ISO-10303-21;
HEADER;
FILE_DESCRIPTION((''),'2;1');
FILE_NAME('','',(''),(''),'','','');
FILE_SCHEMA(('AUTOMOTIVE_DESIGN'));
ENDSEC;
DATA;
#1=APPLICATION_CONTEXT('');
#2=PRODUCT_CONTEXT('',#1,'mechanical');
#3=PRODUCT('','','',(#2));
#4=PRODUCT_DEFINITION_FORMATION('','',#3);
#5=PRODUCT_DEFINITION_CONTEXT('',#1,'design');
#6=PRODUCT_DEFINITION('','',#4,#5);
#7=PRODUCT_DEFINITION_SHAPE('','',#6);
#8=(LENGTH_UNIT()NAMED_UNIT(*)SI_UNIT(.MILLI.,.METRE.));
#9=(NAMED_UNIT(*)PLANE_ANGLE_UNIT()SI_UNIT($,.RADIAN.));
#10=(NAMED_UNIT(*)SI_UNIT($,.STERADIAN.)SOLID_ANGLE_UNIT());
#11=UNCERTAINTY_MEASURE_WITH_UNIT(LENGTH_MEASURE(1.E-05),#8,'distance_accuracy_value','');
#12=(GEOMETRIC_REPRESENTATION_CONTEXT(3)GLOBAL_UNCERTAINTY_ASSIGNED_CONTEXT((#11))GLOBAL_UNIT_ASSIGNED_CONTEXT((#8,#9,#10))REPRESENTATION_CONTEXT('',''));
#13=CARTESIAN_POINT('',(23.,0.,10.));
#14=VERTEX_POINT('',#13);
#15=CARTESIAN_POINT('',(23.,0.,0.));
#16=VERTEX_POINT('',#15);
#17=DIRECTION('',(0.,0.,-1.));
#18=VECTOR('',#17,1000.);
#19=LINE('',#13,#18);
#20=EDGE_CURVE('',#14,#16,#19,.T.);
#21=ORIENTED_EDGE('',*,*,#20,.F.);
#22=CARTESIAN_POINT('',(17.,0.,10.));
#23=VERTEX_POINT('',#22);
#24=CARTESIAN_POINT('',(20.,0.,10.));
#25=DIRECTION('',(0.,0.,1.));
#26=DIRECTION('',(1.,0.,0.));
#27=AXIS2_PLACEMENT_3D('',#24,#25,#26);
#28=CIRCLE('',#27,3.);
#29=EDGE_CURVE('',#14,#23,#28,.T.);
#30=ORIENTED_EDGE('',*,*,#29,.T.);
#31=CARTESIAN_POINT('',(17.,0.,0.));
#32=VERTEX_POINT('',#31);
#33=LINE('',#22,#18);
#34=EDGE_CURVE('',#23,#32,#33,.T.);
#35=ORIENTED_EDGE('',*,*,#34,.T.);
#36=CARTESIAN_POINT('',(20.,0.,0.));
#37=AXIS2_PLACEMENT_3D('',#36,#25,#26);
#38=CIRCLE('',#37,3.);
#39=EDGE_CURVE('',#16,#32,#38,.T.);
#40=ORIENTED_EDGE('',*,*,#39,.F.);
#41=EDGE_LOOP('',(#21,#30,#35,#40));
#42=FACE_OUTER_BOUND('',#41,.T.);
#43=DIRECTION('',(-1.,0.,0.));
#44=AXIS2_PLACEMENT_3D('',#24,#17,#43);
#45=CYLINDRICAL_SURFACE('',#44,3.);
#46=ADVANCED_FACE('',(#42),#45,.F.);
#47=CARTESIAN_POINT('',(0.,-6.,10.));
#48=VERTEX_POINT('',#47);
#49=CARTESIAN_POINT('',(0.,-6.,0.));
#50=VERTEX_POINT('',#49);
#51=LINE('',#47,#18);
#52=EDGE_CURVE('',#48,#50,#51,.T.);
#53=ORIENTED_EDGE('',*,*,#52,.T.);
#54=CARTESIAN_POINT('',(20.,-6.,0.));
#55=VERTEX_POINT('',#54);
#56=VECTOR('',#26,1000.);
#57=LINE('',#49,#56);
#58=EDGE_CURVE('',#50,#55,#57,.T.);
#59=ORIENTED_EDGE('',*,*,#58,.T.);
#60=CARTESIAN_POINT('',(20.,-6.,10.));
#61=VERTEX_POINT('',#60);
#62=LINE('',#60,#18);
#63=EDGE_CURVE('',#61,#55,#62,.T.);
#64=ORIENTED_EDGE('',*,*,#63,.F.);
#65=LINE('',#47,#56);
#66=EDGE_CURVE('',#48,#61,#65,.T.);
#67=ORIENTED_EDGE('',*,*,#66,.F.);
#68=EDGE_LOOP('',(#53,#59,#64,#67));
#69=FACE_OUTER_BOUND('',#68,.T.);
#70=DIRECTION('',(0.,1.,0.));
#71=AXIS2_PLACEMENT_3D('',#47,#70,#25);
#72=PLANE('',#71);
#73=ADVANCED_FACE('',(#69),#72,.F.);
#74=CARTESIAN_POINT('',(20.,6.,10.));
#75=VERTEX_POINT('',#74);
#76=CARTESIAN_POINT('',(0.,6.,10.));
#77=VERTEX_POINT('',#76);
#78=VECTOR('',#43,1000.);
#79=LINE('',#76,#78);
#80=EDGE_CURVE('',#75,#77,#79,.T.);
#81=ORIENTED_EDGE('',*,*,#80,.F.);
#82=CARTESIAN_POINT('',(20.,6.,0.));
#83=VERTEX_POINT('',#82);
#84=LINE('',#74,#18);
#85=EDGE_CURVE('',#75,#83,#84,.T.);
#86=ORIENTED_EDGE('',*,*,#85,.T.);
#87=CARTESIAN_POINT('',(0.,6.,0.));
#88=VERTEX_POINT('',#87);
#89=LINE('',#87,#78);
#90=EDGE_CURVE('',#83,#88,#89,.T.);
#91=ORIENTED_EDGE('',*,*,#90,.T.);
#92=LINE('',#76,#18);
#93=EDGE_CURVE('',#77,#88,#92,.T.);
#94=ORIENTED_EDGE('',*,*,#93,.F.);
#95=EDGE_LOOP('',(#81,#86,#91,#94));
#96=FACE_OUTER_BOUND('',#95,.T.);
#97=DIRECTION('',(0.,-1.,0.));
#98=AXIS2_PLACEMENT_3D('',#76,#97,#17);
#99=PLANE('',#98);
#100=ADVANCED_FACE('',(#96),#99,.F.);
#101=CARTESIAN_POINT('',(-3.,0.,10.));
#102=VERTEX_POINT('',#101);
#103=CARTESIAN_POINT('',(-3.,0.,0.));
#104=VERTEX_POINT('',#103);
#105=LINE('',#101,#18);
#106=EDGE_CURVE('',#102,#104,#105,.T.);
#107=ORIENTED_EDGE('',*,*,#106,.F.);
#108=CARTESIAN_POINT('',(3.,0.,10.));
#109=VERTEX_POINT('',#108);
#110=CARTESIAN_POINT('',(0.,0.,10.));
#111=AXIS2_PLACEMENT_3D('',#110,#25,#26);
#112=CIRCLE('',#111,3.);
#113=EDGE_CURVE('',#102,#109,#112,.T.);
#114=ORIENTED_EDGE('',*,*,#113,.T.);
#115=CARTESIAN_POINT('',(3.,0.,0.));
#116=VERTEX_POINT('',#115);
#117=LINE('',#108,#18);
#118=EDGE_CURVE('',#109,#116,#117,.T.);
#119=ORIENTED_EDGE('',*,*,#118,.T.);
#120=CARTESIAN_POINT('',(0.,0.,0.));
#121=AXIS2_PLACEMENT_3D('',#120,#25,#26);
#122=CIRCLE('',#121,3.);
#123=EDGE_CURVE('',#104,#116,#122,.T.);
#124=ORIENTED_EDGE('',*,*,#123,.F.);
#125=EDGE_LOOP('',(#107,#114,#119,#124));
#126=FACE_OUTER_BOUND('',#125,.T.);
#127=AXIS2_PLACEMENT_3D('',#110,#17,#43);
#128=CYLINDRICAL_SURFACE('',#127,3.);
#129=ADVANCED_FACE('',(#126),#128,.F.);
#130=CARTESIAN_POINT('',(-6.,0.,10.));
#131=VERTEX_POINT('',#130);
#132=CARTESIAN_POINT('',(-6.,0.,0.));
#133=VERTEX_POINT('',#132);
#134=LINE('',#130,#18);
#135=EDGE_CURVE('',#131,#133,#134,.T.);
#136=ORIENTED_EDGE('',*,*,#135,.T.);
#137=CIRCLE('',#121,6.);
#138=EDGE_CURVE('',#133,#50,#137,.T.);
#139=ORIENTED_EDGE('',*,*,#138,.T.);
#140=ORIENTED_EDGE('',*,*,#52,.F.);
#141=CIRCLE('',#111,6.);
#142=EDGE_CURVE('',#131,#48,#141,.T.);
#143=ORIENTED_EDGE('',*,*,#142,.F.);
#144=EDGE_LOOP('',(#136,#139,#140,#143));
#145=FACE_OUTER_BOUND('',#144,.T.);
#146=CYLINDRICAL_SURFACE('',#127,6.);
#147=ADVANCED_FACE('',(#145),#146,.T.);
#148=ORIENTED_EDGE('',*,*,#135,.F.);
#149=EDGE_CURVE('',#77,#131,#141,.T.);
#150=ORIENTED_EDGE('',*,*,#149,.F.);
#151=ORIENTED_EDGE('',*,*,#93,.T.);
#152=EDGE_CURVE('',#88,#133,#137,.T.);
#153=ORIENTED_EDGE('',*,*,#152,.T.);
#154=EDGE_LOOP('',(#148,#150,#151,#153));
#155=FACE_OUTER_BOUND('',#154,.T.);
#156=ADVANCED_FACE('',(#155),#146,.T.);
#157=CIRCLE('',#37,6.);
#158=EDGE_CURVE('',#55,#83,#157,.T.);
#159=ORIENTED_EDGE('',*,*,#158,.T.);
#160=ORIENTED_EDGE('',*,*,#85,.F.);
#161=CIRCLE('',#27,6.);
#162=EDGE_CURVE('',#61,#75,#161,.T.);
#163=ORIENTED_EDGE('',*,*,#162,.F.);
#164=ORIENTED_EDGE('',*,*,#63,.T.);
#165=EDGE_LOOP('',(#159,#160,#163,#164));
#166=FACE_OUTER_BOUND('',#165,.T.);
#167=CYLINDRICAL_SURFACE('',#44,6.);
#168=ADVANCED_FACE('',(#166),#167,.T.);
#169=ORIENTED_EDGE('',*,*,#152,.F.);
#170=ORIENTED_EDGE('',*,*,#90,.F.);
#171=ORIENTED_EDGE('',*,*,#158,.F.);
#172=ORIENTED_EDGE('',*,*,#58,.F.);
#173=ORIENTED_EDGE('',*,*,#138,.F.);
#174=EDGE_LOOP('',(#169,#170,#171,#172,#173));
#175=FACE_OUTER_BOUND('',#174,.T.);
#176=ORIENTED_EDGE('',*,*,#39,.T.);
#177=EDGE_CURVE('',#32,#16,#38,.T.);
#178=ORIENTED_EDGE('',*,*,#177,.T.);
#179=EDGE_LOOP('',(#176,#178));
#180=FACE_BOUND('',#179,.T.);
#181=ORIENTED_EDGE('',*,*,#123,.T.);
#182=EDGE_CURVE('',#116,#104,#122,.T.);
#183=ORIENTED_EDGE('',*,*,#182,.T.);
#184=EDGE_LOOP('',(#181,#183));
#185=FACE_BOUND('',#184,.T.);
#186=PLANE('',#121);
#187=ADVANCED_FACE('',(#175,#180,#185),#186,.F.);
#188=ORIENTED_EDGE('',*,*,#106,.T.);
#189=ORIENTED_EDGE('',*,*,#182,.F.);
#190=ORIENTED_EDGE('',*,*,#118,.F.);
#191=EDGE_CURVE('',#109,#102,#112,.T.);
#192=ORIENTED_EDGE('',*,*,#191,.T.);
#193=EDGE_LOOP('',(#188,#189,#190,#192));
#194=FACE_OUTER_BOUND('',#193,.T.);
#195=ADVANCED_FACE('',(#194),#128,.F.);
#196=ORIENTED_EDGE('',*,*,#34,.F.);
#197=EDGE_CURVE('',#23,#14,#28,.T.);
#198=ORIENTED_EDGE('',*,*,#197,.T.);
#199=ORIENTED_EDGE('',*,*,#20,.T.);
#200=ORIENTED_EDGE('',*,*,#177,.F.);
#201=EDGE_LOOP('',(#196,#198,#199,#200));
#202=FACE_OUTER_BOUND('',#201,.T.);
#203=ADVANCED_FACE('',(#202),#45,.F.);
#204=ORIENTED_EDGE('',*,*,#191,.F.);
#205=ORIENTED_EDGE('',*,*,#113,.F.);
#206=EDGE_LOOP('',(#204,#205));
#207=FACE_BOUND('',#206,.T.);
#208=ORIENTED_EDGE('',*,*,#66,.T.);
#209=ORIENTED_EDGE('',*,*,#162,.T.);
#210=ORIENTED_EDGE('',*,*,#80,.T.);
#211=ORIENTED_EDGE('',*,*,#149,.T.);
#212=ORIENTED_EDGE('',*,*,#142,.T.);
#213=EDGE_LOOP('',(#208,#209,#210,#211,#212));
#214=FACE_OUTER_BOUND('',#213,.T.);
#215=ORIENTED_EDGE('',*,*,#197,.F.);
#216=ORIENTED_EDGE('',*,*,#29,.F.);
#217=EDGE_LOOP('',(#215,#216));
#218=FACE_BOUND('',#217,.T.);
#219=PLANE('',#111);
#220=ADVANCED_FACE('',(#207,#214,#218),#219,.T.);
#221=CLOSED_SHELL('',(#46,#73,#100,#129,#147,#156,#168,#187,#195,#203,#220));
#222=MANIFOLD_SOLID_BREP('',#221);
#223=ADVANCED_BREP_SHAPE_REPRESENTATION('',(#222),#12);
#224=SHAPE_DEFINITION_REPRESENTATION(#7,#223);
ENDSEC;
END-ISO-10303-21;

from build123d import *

# Parameters (mm, degrees)
SKETCH1_R           = 3
BOSS_EXTRUDE1_DEPTH = 10


with BuildPart() as part:
    # Sketch1 → Boss-Extrude1 (new body)
    with BuildSketch(Plane.XY):
        with BuildLine():
            Line((0, -6), (20, -6))
            ThreePointArc((20, -6), (26, 0), (20, 6))
            Line((20, 6), (0, 6))
            ThreePointArc((0, 6), (-6, 0), (0, -6))
        make_face()
        Circle(SKETCH1_R, mode=Mode.SUBTRACT)
        with Locations((20, 0)):
            Circle(SKETCH1_R, mode=Mode.SUBTRACT)
    extrude(amount=BOSS_EXTRUDE1_DEPTH)


solid = part.part
